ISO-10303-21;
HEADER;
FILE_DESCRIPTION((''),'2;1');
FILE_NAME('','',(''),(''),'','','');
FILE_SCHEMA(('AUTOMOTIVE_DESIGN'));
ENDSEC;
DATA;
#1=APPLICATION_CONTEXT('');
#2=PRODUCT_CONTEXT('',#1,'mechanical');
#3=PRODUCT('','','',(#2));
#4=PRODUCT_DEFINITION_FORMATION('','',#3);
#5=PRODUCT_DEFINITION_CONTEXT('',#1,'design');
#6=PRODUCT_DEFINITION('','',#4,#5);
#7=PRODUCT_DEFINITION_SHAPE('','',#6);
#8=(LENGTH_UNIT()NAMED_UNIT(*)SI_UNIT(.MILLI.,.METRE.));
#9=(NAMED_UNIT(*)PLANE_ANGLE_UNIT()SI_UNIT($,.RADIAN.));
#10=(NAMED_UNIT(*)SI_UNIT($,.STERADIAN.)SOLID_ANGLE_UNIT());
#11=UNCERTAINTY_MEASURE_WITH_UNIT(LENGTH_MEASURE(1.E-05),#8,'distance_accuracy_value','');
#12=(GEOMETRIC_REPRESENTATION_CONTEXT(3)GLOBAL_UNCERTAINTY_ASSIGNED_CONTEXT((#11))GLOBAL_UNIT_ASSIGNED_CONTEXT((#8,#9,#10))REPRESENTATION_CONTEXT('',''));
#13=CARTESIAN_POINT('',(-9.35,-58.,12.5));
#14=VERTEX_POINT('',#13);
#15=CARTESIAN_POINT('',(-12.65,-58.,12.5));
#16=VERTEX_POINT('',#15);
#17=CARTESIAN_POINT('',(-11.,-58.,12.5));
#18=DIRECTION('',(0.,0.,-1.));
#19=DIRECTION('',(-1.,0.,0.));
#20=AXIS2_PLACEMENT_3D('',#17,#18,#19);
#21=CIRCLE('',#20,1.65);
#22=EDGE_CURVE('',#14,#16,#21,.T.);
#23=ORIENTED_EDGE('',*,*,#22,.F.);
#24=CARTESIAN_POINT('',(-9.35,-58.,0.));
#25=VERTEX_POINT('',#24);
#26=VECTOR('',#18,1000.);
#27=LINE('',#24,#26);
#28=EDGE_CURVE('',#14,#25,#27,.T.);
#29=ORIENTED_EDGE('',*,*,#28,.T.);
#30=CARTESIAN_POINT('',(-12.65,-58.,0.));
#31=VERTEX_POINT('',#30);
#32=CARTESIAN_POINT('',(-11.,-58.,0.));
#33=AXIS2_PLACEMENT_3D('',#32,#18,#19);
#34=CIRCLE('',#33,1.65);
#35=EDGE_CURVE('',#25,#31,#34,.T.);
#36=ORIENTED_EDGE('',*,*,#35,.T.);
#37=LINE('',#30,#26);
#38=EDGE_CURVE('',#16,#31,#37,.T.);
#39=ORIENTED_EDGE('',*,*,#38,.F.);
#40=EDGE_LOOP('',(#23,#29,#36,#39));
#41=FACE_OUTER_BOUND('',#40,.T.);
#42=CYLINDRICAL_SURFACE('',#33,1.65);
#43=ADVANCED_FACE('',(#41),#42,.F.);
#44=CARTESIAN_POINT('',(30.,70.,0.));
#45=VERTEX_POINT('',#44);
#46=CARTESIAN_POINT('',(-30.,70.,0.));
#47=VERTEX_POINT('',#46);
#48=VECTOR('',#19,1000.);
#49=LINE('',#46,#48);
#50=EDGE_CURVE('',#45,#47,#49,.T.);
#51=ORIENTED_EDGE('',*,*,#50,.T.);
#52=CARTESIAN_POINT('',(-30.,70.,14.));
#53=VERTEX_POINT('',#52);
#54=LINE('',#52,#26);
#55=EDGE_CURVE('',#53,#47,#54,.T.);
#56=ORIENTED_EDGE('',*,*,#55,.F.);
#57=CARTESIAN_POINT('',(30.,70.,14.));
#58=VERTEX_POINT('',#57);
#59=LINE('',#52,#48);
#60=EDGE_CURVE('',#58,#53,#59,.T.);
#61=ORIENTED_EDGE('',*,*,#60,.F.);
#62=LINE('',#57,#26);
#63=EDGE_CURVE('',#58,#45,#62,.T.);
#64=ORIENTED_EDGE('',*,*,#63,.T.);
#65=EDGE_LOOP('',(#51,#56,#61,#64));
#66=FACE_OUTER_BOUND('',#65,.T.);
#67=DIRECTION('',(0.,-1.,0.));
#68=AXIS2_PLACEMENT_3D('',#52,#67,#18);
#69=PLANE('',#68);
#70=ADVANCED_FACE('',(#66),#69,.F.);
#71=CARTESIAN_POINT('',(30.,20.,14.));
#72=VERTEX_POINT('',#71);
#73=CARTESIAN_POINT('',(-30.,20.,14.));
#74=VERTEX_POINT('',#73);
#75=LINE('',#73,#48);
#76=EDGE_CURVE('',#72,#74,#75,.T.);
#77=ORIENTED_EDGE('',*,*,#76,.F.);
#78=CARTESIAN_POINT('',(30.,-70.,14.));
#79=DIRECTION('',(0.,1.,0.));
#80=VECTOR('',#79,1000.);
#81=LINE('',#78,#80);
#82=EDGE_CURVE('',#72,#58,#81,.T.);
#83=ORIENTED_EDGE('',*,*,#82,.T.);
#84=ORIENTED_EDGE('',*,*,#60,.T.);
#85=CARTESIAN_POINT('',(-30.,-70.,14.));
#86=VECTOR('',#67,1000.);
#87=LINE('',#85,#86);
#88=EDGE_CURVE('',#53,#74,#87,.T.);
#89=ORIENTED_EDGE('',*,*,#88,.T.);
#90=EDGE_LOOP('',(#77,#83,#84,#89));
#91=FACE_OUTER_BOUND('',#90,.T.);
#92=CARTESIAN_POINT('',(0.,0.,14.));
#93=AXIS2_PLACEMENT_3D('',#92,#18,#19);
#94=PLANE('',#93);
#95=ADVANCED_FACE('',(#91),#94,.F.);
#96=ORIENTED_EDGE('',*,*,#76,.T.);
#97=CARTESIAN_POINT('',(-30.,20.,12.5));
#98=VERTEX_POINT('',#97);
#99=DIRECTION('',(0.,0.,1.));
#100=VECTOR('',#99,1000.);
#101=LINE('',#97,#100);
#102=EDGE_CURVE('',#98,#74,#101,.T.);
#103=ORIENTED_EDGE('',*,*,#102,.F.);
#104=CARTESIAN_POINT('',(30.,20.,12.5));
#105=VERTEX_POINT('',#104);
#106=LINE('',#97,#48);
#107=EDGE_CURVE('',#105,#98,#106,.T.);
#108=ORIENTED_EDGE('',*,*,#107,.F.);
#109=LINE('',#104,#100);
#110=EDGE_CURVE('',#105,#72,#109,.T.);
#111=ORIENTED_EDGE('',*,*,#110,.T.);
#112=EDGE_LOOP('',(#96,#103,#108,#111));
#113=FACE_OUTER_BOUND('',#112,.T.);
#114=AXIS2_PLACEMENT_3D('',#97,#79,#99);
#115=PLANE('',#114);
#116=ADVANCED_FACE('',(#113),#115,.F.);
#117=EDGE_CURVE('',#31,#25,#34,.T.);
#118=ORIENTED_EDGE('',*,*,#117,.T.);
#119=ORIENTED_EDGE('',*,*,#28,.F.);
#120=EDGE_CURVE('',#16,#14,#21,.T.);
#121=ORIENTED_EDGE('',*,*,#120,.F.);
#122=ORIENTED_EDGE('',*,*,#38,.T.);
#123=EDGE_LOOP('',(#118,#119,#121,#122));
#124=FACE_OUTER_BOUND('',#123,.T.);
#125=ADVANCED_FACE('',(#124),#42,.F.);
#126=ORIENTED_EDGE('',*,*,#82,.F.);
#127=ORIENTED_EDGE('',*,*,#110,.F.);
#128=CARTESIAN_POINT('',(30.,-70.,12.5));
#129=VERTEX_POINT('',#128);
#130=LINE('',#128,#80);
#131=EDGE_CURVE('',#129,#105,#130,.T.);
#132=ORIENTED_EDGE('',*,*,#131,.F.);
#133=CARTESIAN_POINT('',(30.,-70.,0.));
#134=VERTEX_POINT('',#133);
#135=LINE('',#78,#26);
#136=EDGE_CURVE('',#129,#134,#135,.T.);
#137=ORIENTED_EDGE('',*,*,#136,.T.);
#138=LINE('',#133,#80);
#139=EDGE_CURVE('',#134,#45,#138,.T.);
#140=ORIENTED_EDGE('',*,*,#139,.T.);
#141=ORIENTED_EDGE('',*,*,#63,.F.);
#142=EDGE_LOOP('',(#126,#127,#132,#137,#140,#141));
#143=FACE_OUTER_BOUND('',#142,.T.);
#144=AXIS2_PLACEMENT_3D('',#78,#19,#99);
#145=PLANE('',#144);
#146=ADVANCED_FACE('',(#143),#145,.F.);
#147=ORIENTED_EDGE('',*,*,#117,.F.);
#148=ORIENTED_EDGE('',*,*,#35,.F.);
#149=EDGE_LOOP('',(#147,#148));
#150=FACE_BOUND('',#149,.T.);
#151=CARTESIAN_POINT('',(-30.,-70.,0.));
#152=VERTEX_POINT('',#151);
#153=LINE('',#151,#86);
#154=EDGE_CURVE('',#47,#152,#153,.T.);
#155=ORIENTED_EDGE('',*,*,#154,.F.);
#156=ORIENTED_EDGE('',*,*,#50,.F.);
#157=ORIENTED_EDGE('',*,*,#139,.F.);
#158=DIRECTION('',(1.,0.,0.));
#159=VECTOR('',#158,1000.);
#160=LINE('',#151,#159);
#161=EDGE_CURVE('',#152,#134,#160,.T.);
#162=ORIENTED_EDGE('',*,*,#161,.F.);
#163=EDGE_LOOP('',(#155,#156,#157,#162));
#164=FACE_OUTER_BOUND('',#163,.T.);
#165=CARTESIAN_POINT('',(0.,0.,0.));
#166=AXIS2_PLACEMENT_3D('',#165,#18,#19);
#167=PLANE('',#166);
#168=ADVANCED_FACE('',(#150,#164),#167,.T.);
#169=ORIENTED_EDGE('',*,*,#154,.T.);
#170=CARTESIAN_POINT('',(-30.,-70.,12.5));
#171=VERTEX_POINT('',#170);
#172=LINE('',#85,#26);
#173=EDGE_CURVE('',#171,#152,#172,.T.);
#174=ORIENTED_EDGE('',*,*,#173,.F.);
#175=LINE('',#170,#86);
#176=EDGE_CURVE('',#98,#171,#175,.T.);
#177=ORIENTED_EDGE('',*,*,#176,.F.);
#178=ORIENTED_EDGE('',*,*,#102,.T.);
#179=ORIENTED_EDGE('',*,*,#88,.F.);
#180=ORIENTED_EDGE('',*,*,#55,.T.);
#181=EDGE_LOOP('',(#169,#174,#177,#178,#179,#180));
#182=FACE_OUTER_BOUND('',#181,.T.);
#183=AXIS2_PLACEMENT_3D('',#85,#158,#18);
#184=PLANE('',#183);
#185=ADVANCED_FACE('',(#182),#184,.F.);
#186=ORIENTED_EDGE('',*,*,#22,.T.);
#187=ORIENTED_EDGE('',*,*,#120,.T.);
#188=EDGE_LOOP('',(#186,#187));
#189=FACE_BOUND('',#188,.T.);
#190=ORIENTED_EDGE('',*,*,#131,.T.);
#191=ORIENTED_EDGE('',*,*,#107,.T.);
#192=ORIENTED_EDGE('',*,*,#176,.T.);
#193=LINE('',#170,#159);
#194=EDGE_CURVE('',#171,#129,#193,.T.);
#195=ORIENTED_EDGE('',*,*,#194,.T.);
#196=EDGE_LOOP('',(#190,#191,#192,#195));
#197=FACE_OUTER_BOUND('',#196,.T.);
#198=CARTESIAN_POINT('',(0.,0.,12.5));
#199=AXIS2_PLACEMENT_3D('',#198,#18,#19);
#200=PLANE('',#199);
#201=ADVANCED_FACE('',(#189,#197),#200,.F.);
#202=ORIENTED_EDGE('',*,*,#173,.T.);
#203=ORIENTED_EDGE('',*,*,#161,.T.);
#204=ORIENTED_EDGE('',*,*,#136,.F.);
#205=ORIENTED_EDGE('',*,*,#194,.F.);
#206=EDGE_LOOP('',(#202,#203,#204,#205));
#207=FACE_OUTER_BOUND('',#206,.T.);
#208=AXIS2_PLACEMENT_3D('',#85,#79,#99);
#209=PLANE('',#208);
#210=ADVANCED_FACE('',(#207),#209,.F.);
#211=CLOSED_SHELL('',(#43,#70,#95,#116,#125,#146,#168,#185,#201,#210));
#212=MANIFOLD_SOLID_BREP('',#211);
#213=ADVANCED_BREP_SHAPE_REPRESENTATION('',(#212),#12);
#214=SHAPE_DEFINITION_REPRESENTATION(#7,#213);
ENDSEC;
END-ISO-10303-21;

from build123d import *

# Parameters (mm, degrees)
SKETCH_1_W          = 60
SKETCH_1_H          = 140
EXTRUDE_1_DEPTH     = 14
SKETCH_2_W          = 60
SKETCH_2_H          = 90
CUT_EXTRUDE_1_DEPTH = 1.5
HOLE_WIZARD_M4_1_D  = 3.3


with BuildPart() as part:
    # 草图1 → 凸台-拉伸1 (new body)
    with BuildSketch(Plane.XY):
        Rectangle(SKETCH_1_W, SKETCH_1_H)
    extrude(amount=EXTRUDE_1_DEPTH)

    # 草图2 → 切除-拉伸1 (cut)
    with BuildSketch(Plane.XY.offset(14)):
        with Locations((0, -25)):
            Rectangle(SKETCH_2_W, SKETCH_2_H)
    extrude(amount=-CUT_EXTRUDE_1_DEPTH, mode=Mode.SUBTRACT)

    # M4 螺纹孔1 (through all)
    with Locations(Plane(origin=(0, 0, 0), x_dir=(-1, 0, 0), z_dir=(0, 0, -1))):
        with Locations((11, -58)):
            Hole(HOLE_WIZARD_M4_1_D / 2)


solid = part.part
